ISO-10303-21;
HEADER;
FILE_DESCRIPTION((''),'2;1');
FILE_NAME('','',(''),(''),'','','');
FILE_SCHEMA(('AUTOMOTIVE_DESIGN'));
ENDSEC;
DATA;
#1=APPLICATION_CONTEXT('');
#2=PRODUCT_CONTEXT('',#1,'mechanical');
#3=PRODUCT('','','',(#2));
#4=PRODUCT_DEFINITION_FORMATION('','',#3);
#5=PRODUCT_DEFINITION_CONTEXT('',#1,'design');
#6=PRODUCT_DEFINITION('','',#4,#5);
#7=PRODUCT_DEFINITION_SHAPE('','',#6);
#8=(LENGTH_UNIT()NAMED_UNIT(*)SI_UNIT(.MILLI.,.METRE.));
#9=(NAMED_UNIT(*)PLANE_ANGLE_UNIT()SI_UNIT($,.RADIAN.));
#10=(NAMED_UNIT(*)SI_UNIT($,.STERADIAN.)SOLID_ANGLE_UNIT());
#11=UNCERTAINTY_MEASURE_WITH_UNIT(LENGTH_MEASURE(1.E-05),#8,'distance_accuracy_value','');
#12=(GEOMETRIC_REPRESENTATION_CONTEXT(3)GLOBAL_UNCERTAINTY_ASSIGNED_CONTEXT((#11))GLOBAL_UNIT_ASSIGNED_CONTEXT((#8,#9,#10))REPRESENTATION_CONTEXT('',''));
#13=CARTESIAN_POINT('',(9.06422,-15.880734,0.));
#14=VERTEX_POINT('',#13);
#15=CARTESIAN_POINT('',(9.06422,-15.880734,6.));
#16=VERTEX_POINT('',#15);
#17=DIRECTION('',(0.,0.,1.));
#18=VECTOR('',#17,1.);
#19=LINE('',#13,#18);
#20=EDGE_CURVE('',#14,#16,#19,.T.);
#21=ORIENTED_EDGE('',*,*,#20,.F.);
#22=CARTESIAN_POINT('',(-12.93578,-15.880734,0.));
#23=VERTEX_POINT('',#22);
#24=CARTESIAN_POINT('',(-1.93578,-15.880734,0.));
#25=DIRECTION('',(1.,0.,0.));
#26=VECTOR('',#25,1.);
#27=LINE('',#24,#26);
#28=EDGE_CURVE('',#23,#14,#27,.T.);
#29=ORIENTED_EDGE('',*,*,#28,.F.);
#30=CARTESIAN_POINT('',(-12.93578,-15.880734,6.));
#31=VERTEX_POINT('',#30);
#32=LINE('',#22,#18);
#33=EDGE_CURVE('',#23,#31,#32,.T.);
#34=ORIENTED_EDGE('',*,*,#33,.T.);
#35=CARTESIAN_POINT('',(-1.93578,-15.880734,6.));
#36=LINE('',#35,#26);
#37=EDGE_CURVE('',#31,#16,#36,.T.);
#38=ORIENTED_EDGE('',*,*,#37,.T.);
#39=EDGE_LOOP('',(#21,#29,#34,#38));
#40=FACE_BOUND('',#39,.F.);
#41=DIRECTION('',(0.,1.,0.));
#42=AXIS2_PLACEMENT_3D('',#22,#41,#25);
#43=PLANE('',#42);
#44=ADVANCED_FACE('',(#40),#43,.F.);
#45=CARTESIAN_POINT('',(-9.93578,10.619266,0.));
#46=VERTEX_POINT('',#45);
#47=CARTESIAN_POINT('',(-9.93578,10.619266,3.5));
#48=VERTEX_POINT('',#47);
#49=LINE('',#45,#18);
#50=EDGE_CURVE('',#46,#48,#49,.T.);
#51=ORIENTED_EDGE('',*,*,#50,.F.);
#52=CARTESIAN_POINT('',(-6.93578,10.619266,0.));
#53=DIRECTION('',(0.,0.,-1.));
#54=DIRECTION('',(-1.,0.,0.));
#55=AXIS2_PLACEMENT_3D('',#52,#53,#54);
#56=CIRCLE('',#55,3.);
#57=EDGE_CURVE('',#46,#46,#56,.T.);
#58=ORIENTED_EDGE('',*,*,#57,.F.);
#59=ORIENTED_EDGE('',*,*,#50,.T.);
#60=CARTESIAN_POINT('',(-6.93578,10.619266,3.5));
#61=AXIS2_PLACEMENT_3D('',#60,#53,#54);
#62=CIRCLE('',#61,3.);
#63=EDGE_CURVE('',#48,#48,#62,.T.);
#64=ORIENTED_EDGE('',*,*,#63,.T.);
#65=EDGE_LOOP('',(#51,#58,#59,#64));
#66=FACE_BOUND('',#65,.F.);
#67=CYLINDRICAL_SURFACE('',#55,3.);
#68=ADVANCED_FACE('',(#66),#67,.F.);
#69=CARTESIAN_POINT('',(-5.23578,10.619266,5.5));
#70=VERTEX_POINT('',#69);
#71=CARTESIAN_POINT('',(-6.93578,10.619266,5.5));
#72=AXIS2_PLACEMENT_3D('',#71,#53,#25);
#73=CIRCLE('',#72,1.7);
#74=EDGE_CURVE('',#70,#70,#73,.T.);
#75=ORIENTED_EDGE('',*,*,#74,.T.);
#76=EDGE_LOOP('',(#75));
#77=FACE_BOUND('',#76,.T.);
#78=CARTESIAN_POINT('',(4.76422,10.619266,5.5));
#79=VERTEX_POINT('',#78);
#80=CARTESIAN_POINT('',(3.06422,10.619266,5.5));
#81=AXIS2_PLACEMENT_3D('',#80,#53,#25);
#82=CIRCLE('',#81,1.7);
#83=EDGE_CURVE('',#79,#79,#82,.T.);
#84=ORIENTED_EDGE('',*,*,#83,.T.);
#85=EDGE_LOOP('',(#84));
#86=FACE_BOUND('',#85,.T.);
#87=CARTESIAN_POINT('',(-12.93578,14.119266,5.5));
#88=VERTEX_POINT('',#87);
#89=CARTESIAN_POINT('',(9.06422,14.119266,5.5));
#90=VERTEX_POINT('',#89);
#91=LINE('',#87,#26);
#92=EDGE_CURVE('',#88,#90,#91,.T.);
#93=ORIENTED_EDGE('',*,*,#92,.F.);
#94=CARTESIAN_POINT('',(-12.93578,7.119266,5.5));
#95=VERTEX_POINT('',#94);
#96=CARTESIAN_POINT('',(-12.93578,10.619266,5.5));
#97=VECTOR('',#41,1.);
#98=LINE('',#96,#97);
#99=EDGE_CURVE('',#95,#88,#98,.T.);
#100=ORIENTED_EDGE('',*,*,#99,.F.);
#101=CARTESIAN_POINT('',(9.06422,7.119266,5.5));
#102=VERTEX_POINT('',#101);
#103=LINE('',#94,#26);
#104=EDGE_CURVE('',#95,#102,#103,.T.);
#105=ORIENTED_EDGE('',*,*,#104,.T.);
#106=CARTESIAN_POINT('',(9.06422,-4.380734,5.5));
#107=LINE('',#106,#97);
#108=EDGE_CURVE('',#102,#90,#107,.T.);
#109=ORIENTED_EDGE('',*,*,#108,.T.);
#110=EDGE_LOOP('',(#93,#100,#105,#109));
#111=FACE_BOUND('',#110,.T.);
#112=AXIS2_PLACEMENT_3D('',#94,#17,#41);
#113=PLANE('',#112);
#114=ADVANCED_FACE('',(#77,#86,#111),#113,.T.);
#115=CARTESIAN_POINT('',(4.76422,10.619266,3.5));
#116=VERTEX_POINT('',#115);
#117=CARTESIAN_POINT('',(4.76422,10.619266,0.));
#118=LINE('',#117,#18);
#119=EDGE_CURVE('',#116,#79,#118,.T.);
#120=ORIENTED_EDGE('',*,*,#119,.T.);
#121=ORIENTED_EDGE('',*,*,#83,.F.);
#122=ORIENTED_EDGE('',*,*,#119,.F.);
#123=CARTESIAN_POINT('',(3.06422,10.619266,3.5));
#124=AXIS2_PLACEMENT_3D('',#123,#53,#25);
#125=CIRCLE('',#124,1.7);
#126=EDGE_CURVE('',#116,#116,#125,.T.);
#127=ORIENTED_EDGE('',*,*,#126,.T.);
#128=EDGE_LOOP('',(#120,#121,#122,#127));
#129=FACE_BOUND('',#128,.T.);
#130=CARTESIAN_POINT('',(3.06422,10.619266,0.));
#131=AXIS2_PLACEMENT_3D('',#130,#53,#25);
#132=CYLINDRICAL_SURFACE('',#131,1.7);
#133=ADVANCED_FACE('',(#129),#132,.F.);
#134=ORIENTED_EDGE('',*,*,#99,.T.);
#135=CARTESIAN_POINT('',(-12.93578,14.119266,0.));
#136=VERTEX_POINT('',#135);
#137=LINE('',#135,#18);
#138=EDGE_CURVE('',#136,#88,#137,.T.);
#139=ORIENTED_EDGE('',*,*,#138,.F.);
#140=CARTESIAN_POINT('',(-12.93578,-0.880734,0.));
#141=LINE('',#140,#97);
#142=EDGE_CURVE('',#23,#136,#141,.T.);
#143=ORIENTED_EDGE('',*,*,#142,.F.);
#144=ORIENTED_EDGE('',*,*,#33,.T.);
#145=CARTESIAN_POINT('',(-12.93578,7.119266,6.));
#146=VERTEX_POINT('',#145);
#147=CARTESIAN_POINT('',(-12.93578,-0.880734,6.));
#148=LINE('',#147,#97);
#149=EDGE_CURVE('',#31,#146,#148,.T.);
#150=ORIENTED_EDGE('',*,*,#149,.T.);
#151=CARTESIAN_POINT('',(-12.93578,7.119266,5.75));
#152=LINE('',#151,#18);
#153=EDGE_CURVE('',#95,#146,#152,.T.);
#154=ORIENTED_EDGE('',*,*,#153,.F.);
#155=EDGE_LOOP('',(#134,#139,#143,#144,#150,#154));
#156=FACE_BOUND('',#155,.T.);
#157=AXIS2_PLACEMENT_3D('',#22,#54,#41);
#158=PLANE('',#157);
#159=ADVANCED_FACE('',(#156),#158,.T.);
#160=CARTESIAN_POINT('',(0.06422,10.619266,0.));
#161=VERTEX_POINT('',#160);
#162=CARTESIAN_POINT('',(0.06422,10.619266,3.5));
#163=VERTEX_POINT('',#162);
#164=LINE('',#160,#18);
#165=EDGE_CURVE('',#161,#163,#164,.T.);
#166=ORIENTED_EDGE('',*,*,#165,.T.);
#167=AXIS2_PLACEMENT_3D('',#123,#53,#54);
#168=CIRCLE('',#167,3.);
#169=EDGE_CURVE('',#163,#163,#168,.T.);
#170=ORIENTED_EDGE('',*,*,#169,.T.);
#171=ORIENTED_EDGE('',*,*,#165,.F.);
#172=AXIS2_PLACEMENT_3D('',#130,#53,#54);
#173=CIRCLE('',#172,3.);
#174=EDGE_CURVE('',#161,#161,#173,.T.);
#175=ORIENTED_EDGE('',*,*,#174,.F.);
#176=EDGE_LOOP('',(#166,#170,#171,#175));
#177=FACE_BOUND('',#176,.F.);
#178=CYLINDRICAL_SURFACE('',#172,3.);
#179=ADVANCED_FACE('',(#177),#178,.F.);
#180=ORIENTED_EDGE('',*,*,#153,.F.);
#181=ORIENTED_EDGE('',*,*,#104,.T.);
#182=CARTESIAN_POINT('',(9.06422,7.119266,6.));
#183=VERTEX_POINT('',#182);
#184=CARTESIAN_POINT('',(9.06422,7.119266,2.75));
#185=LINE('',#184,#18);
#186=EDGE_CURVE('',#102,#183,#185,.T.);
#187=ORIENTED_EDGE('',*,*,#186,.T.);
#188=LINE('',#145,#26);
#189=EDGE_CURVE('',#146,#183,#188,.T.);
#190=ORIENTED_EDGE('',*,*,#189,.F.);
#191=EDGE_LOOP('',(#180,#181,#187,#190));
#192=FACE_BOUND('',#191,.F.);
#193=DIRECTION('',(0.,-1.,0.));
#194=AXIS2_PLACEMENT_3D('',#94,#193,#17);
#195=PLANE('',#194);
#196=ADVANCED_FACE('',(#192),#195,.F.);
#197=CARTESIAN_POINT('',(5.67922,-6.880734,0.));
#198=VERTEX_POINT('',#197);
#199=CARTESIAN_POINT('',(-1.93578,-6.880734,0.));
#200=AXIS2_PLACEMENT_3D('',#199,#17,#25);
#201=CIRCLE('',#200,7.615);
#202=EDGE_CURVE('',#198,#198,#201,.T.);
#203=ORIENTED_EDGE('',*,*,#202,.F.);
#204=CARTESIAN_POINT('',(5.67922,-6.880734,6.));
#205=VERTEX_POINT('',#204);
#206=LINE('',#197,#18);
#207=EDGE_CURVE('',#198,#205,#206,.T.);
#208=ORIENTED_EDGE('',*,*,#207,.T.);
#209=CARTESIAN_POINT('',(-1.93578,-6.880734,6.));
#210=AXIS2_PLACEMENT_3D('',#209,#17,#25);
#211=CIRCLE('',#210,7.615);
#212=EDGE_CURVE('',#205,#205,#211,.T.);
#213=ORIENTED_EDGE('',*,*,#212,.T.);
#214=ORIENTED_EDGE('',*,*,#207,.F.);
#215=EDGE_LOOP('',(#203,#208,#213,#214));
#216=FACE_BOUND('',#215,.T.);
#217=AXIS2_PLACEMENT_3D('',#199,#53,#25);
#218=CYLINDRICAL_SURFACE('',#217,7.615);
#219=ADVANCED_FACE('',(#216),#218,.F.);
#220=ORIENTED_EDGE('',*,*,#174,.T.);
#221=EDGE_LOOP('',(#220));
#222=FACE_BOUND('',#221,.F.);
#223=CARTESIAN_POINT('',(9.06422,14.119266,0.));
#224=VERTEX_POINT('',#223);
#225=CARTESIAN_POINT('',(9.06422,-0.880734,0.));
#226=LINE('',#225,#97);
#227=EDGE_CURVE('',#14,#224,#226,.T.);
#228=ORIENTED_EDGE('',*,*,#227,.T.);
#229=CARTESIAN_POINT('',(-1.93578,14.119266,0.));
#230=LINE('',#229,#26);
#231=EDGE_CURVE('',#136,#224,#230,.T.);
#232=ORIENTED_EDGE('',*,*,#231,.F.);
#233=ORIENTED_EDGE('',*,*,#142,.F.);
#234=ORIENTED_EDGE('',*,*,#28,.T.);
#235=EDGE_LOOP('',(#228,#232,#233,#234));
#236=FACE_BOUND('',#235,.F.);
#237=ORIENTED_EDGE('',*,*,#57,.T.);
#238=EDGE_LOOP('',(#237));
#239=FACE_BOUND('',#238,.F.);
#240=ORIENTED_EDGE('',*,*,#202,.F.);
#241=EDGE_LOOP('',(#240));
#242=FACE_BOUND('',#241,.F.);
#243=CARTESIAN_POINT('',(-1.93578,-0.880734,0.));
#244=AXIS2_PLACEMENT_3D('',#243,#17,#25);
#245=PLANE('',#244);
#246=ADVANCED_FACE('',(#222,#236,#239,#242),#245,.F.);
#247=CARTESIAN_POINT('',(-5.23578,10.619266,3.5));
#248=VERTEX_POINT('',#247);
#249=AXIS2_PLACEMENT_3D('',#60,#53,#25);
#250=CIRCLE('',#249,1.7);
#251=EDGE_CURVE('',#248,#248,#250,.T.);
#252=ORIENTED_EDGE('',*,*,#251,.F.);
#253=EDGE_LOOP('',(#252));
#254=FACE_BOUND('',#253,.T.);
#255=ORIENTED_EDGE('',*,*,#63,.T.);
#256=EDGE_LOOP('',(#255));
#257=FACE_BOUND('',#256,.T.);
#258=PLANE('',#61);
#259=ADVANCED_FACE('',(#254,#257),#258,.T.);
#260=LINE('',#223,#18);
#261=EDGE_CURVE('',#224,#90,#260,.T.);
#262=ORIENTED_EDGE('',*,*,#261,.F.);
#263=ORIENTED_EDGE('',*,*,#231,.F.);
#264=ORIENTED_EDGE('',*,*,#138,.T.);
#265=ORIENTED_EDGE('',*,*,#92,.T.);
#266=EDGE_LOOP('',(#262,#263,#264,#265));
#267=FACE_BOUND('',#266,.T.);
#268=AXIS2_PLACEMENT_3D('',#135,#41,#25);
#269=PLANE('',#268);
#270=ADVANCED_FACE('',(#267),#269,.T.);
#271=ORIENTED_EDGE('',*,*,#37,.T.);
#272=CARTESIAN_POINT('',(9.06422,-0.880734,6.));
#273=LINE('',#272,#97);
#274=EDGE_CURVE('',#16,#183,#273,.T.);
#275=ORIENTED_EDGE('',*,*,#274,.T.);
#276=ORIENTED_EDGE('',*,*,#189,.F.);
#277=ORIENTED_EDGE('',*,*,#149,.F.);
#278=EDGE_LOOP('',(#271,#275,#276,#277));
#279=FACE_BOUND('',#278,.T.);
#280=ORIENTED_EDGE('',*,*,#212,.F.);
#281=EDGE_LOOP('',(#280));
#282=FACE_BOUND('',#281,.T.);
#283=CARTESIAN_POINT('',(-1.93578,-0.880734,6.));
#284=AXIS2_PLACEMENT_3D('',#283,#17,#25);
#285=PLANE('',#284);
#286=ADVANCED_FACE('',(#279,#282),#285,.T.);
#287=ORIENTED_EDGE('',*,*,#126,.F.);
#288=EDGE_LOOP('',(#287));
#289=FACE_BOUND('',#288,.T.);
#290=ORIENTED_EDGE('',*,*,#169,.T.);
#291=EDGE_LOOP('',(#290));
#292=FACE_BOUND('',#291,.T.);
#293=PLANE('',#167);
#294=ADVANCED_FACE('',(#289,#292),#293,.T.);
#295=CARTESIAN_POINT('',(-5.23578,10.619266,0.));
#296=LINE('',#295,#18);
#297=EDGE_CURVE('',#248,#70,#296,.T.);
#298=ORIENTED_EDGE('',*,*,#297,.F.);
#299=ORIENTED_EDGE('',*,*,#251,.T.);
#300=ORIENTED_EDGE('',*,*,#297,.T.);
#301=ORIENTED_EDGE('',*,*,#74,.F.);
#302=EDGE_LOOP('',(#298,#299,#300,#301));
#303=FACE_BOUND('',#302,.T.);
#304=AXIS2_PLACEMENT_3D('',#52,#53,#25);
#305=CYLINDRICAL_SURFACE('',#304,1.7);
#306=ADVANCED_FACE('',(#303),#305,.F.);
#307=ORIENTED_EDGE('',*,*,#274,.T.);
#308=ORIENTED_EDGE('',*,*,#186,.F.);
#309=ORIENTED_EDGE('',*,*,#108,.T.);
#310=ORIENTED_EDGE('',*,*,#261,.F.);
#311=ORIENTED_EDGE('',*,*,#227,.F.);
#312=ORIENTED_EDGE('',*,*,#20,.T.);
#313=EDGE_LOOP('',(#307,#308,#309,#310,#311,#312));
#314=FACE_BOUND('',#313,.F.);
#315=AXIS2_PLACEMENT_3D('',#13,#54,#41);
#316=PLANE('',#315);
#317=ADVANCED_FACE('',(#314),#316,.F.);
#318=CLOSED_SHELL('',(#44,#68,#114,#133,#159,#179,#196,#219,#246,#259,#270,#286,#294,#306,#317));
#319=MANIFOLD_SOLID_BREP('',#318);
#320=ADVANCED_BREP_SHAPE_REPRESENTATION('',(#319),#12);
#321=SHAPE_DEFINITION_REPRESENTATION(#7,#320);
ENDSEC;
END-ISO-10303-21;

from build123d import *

# Parameters (mm, degrees)
SKETCH_1_W          = 22
SKETCH_1_H          = 30
SKETCH_1_R          = 7.615
SKETCH_1_R_2        = 1.7
EXTRUDE_1_DEPTH     = 6
SKETCH_3_W          = 0.5
SKETCH_3_H          = 7
CUT_EXTRUDE_1_DEPTH = 28.788445632
SKETCH_4_R          = 3
CUT_EXTRUDE_2_DEPTH = 3.5


with BuildPart() as part:
    # 草图1 → 凸台-拉伸1 (new body)
    with BuildSketch(Plane.XY):
        with Locations((-1.935779817, -0.880733945)):
            Rectangle(SKETCH_1_W, SKETCH_1_H)
        with Locations((-1.935779817, -6.880733945)):
            Circle(SKETCH_1_R, mode=Mode.SUBTRACT)
        with Locations((-6.935779817, 10.619266055)):
            Circle(SKETCH_1_R_2, mode=Mode.SUBTRACT)
        with Locations((3.064220183, 10.619266055)):
            Circle(SKETCH_1_R_2, mode=Mode.SUBTRACT)
    extrude(amount=EXTRUDE_1_DEPTH)

    # 草图3 → 切除-拉伸1 (cut, through all)
    with BuildSketch(Plane.ZY.offset(12.935779817)):
        with Locations((5.75, 10.619266055)):
            Rectangle(SKETCH_3_W, SKETCH_3_H)
    extrude(amount=-CUT_EXTRUDE_1_DEPTH, mode=Mode.SUBTRACT)

    # 草图4 → 切除-拉伸2 (cut)
    with BuildSketch(Plane(origin=(0, 0, 0), x_dir=(-1, 0, 0), z_dir=(0, 0, -1))):
        with Locations((-3.064220183, 10.619266055)):
            Circle(SKETCH_4_R)
        with Locations((6.935779817, 10.619266055)):
            Circle(SKETCH_4_R)
    extrude(amount=-CUT_EXTRUDE_2_DEPTH, mode=Mode.SUBTRACT)


solid = part.part
